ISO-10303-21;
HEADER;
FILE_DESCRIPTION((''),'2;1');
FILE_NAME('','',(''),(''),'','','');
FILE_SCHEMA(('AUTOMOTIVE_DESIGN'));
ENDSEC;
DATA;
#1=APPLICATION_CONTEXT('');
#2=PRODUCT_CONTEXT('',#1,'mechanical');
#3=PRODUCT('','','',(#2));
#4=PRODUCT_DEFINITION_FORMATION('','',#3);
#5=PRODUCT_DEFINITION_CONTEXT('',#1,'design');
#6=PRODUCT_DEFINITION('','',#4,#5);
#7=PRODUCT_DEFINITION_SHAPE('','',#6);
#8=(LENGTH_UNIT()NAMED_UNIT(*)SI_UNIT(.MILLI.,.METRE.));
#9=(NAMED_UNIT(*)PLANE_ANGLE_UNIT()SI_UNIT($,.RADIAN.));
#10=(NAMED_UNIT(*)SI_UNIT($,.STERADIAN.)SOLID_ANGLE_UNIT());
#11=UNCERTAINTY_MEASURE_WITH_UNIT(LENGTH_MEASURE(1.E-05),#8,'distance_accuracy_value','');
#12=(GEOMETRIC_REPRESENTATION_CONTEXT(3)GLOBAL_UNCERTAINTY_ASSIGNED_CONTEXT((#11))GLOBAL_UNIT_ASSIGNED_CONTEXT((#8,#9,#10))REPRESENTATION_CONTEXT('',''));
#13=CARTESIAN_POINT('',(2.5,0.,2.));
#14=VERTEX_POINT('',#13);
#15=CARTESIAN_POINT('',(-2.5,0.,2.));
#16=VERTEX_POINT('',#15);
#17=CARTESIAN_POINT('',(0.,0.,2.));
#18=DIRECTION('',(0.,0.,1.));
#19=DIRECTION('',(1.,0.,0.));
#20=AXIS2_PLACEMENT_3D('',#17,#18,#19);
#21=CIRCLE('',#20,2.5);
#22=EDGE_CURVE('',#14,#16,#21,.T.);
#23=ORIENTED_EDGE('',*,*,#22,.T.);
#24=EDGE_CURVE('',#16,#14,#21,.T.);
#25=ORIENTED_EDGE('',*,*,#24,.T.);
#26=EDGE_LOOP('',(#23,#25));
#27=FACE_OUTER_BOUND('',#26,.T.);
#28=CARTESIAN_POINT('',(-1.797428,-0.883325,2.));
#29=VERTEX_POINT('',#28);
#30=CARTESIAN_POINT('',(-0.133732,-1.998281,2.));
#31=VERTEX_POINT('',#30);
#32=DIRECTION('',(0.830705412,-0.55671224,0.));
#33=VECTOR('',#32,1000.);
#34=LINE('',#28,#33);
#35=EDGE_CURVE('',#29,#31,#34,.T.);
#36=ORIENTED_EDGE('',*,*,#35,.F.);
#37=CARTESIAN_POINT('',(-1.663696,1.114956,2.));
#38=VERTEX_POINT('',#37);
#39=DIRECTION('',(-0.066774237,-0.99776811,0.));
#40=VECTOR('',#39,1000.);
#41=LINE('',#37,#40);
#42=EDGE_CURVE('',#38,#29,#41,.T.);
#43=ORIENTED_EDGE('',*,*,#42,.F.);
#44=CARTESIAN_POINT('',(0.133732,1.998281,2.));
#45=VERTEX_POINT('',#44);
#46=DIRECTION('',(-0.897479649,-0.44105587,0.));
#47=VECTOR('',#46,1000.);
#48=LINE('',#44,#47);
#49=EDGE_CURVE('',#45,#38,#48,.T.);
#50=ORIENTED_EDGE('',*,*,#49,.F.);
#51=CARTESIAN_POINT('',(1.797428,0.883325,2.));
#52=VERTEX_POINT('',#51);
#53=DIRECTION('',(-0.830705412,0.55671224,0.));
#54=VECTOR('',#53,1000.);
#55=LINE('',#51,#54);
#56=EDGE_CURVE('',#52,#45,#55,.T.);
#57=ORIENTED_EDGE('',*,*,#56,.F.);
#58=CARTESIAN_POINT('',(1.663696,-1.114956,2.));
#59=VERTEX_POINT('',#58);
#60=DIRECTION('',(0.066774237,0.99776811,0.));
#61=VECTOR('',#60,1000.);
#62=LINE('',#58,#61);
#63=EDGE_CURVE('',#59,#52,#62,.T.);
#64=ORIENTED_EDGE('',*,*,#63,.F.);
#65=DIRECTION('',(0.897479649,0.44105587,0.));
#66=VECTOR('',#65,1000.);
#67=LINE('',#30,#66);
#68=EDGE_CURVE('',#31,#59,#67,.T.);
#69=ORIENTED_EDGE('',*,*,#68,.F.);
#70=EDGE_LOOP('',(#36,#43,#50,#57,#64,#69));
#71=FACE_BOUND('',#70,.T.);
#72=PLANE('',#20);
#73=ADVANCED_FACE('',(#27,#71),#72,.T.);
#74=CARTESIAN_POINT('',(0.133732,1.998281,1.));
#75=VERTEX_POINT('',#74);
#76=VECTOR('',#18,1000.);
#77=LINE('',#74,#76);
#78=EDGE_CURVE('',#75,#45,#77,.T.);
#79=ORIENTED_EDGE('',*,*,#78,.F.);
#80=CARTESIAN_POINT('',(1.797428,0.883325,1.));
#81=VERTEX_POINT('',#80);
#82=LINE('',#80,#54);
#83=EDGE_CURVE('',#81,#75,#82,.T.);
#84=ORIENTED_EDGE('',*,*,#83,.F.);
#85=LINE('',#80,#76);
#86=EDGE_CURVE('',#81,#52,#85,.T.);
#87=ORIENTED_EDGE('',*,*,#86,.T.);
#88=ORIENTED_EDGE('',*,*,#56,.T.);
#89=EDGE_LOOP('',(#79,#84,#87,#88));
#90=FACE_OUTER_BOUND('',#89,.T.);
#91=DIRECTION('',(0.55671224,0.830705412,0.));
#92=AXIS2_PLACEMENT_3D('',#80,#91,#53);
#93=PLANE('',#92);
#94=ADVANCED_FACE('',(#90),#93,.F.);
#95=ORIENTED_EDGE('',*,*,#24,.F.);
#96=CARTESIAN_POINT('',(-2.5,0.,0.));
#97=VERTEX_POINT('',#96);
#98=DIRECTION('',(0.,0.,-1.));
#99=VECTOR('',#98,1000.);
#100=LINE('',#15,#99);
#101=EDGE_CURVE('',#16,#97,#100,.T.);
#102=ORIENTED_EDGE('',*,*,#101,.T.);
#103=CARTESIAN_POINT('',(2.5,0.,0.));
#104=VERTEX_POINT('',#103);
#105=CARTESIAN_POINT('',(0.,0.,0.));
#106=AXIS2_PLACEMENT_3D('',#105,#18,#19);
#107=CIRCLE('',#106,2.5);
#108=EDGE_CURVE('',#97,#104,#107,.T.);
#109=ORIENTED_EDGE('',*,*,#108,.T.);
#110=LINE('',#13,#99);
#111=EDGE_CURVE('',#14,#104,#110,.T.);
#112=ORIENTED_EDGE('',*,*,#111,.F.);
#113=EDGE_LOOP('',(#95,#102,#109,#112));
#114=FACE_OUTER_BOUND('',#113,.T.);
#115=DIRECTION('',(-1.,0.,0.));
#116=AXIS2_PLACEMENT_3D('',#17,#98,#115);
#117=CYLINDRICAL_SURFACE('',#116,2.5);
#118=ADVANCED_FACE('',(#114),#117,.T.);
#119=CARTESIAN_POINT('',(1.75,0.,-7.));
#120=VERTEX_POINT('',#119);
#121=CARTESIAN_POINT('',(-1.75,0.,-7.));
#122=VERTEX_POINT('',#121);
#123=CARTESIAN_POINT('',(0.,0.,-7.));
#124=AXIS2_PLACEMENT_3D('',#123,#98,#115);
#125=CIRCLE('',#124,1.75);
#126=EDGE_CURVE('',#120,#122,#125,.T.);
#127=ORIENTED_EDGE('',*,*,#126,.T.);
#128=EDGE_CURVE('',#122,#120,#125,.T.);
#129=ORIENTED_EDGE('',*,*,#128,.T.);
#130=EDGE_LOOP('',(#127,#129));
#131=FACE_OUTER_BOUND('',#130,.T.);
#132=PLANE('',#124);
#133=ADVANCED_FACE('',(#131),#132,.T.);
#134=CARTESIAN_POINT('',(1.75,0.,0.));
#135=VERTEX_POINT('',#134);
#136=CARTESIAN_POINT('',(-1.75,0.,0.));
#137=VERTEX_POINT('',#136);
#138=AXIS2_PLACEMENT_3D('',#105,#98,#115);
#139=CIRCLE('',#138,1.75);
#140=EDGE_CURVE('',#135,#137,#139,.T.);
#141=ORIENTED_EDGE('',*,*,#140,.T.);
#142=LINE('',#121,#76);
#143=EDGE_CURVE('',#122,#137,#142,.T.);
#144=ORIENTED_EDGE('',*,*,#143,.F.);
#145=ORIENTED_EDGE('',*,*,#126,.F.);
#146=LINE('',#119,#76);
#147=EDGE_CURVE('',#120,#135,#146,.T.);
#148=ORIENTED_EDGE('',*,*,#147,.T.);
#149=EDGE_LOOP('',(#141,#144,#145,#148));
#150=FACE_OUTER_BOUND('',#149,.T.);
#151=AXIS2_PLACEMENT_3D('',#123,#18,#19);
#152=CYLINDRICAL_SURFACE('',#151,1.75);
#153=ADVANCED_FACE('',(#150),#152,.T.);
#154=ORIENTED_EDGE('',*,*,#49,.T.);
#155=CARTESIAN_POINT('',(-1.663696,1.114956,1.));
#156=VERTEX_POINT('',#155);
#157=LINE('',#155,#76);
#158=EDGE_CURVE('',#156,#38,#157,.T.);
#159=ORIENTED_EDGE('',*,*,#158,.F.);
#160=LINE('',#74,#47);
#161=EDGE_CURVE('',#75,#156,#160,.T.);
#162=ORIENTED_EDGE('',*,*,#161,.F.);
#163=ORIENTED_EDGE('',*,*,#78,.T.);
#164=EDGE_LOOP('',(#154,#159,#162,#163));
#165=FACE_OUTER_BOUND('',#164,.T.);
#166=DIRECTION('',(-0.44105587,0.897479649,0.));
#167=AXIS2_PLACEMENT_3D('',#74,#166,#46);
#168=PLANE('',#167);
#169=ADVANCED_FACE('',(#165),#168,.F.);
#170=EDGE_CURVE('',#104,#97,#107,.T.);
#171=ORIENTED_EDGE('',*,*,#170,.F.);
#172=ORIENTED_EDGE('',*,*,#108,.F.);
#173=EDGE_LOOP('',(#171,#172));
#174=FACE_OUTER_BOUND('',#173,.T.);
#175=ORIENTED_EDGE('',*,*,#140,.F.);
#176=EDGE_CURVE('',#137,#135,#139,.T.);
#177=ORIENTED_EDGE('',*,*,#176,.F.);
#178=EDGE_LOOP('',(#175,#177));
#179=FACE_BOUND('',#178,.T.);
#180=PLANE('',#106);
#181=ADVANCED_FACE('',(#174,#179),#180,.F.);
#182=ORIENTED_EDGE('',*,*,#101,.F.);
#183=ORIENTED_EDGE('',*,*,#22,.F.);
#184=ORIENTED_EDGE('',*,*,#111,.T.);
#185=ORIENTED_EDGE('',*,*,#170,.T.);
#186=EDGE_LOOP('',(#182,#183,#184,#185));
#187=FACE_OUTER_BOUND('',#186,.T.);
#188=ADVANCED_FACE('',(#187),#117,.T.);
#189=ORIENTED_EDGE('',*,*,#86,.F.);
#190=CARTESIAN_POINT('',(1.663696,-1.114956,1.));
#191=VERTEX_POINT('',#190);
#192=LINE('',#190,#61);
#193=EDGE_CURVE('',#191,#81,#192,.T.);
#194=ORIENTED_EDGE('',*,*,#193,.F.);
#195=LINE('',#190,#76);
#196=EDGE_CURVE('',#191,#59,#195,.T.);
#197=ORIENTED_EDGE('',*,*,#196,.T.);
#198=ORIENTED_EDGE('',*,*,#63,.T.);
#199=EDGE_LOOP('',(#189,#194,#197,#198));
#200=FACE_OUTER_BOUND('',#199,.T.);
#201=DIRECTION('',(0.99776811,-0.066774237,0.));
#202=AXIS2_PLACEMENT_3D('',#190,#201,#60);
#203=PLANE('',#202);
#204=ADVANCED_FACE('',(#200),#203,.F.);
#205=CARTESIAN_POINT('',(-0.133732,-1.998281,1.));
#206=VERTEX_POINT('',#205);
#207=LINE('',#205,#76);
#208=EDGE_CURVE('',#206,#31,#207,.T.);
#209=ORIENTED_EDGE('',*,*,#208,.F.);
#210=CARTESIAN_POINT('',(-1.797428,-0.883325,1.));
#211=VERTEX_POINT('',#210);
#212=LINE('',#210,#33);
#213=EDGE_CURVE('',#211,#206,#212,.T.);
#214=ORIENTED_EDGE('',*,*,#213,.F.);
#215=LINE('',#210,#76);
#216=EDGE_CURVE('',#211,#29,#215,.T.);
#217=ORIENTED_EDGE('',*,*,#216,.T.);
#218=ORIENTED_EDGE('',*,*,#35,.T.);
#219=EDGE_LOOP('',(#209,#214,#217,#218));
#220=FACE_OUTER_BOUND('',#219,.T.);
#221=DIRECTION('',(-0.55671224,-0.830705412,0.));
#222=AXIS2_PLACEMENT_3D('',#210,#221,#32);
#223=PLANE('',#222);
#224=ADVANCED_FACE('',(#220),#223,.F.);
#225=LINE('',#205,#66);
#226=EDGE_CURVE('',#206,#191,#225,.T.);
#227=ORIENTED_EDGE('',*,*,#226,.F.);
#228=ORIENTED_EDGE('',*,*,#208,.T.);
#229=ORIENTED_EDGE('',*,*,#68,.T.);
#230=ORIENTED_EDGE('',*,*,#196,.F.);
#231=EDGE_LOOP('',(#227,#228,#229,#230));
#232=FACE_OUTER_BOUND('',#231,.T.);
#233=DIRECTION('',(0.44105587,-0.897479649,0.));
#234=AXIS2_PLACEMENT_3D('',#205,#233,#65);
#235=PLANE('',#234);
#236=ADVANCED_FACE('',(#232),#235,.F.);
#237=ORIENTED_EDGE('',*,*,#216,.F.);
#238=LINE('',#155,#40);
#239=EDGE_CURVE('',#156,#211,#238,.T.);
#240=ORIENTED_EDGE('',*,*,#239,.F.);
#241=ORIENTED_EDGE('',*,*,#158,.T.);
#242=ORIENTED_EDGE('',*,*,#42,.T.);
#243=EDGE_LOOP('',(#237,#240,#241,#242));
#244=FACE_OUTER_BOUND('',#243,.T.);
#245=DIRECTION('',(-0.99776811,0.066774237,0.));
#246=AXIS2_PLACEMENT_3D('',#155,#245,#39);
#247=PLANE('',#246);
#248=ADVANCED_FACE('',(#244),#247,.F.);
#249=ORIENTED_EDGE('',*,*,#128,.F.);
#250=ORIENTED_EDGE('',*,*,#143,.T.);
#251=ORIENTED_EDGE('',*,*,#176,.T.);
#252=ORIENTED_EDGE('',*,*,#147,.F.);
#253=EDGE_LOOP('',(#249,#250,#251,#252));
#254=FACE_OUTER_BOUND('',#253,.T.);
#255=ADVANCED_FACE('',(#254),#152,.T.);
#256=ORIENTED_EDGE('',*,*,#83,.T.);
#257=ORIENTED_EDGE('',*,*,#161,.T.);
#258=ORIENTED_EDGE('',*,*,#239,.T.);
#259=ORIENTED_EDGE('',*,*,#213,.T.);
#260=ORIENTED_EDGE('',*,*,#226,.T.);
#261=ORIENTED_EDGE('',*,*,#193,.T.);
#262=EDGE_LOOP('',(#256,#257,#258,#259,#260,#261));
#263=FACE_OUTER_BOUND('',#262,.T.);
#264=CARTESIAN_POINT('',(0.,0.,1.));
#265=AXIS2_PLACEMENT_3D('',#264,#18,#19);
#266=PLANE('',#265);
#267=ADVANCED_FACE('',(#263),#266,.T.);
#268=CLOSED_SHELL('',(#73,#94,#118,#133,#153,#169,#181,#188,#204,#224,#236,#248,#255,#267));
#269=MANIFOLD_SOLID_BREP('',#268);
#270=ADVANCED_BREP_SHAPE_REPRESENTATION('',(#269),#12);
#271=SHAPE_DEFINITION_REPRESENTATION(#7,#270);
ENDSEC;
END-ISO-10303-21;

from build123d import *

# Parameters (mm, degrees)
SKETCH1_R           = 2.5
BOSS_EXTRUDE1_DEPTH = 2
CUT_EXTRUDE1_DEPTH  = 1
SKETCH3_R           = 1.75
BOSS_EXTRUDE2_DEPTH = 7


with BuildPart() as part:
    # Sketch1 → Boss-Extrude1 (new body)
    with BuildSketch(Plane.XY):
        Circle(SKETCH1_R)
    extrude(amount=BOSS_EXTRUDE1_DEPTH)

    # Sketch2 → Cut-Extrude1 (cut)
    with BuildSketch(Plane.XY.offset(2)):
        Polygon((1.663695781, -1.114955786), (1.797427926, 0.883324918), (0.133732144, 1.998280704), (-1.663695781, 1.114955786), (-1.797427926, -0.883324918), (-0.133732144, -1.998280704), align=None)
    extrude(amount=-CUT_EXTRUDE1_DEPTH, mode=Mode.SUBTRACT)

    # Sketch3 → Boss-Extrude2 (add)
    with BuildSketch(Plane(origin=(0, 0, 0), x_dir=(-1, 0, 0), z_dir=(0, 0, -1))):
        Circle(SKETCH3_R)
    extrude(amount=BOSS_EXTRUDE2_DEPTH)


solid = part.part
